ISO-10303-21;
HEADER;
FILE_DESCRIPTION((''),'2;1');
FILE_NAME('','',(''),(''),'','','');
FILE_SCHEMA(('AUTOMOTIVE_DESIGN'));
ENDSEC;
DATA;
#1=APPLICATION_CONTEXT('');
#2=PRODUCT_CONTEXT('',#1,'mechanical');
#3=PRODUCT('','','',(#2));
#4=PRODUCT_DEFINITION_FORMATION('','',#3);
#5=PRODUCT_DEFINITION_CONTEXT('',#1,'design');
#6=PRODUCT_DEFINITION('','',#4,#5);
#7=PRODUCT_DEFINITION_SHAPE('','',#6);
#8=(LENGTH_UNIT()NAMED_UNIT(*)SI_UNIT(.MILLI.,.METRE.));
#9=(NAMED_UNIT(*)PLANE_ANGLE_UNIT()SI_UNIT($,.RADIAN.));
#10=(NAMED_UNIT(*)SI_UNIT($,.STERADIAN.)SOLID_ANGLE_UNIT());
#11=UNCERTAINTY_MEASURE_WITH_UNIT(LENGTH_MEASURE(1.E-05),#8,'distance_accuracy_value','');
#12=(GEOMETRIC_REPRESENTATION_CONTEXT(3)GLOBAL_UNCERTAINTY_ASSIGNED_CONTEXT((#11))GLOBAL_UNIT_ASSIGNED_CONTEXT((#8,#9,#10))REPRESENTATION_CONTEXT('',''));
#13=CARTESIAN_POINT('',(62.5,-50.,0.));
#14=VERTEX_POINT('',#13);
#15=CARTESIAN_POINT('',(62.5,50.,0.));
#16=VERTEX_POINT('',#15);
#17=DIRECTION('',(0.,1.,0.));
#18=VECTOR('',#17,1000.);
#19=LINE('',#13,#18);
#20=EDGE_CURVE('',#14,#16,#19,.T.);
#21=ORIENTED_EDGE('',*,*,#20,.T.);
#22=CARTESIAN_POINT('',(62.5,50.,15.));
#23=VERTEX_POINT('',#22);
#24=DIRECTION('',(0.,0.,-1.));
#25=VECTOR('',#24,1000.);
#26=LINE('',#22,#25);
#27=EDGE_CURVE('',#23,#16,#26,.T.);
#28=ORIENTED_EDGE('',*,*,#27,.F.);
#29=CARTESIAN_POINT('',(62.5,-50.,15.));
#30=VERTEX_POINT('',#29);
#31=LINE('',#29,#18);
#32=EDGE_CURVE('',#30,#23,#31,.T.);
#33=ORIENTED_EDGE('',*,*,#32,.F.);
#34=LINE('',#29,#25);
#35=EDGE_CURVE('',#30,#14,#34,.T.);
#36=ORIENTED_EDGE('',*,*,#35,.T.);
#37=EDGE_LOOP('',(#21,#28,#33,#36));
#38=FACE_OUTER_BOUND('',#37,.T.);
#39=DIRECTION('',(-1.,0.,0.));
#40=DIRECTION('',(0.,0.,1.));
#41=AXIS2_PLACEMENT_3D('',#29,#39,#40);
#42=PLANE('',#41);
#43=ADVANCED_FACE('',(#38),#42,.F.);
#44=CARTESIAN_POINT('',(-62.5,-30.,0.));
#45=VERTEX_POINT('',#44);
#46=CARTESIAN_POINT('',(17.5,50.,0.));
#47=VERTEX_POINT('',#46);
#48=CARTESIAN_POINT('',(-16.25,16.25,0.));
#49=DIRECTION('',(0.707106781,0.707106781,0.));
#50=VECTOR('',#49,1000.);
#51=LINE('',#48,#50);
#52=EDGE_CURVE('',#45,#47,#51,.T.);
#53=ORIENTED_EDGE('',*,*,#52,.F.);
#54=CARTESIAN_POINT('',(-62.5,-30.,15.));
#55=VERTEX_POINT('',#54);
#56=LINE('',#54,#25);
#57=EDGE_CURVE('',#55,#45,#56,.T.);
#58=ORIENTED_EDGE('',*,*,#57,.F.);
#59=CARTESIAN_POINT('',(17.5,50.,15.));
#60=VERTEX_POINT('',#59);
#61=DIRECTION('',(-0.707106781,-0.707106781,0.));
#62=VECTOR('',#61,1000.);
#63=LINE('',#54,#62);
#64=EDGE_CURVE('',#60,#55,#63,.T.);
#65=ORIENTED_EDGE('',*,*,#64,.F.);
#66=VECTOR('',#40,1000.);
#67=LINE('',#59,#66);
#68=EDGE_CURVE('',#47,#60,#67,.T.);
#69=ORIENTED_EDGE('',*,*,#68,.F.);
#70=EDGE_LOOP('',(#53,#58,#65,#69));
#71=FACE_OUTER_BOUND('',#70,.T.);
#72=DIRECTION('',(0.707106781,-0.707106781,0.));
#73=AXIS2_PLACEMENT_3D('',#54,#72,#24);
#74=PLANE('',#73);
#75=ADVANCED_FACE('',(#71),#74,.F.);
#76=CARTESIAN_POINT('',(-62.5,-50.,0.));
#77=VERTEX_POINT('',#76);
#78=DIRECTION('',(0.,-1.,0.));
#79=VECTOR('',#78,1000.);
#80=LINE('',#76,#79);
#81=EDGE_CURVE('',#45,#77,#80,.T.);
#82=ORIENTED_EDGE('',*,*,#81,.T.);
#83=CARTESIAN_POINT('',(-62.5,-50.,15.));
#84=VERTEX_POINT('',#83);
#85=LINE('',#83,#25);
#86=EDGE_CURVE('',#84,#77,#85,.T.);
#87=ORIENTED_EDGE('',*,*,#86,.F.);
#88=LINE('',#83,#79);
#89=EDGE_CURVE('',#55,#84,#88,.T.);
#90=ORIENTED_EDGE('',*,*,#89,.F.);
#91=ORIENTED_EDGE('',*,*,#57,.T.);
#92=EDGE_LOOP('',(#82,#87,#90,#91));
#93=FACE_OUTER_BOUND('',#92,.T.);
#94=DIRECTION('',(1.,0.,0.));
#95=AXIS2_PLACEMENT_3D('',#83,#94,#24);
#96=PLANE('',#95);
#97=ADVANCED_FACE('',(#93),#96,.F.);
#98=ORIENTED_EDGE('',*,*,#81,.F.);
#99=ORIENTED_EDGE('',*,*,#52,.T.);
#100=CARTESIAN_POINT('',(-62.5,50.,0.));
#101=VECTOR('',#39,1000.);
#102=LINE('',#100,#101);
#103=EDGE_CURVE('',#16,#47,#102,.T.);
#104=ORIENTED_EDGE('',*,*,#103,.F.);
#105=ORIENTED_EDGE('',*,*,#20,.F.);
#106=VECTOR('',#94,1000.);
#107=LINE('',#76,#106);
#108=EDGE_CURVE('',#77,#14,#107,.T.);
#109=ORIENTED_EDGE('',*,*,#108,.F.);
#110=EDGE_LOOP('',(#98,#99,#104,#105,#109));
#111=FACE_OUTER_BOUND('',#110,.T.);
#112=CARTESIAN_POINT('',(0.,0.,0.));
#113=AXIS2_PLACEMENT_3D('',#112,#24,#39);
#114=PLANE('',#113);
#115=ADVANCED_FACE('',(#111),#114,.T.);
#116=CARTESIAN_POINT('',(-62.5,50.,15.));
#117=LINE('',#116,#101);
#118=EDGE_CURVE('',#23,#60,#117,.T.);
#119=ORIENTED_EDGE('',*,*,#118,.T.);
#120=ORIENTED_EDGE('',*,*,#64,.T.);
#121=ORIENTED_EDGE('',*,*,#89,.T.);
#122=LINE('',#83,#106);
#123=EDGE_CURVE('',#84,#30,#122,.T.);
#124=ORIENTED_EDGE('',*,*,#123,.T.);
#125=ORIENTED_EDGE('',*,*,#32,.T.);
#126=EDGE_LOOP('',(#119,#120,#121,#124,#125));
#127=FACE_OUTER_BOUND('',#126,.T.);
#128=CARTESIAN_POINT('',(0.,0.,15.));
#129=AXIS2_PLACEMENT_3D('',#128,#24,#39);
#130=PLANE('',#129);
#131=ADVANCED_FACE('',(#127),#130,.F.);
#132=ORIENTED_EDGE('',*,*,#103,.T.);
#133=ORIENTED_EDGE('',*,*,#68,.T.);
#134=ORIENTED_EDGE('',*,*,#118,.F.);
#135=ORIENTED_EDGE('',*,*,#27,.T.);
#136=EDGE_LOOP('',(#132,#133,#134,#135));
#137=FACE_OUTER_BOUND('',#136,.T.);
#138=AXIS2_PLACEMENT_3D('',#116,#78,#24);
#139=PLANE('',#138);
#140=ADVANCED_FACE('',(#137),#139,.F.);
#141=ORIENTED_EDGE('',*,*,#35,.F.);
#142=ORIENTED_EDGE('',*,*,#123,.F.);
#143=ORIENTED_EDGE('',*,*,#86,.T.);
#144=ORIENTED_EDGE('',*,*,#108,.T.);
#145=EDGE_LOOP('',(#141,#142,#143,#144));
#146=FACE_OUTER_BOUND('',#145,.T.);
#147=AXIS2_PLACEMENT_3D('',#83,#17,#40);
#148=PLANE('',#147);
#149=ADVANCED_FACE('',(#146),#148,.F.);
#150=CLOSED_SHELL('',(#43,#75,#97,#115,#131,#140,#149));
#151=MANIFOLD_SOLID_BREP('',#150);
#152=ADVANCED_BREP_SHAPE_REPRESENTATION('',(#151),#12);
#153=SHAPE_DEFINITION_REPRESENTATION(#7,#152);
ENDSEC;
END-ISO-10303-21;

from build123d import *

# Parameters (mm, degrees)
SKETCH_1_W      = 125
SKETCH_1_H      = 100
EXTRUDE_1_DEPTH = 15
CHAMFER_1_SIZE  = 80


with BuildPart() as part:
    # 草图1 → 凸台-拉伸1 (new body)
    with BuildSketch(Plane.XY):
        Rectangle(SKETCH_1_W, SKETCH_1_H)
    extrude(amount=EXTRUDE_1_DEPTH)

    # 倒角1
    chamfer_1_edges = [part.edges().sort_by_distance(p)[0] for p in [
        (-62.5, 50, 7.5),
    ]]
    chamfer(chamfer_1_edges, length=CHAMFER_1_SIZE)


solid = part.part
